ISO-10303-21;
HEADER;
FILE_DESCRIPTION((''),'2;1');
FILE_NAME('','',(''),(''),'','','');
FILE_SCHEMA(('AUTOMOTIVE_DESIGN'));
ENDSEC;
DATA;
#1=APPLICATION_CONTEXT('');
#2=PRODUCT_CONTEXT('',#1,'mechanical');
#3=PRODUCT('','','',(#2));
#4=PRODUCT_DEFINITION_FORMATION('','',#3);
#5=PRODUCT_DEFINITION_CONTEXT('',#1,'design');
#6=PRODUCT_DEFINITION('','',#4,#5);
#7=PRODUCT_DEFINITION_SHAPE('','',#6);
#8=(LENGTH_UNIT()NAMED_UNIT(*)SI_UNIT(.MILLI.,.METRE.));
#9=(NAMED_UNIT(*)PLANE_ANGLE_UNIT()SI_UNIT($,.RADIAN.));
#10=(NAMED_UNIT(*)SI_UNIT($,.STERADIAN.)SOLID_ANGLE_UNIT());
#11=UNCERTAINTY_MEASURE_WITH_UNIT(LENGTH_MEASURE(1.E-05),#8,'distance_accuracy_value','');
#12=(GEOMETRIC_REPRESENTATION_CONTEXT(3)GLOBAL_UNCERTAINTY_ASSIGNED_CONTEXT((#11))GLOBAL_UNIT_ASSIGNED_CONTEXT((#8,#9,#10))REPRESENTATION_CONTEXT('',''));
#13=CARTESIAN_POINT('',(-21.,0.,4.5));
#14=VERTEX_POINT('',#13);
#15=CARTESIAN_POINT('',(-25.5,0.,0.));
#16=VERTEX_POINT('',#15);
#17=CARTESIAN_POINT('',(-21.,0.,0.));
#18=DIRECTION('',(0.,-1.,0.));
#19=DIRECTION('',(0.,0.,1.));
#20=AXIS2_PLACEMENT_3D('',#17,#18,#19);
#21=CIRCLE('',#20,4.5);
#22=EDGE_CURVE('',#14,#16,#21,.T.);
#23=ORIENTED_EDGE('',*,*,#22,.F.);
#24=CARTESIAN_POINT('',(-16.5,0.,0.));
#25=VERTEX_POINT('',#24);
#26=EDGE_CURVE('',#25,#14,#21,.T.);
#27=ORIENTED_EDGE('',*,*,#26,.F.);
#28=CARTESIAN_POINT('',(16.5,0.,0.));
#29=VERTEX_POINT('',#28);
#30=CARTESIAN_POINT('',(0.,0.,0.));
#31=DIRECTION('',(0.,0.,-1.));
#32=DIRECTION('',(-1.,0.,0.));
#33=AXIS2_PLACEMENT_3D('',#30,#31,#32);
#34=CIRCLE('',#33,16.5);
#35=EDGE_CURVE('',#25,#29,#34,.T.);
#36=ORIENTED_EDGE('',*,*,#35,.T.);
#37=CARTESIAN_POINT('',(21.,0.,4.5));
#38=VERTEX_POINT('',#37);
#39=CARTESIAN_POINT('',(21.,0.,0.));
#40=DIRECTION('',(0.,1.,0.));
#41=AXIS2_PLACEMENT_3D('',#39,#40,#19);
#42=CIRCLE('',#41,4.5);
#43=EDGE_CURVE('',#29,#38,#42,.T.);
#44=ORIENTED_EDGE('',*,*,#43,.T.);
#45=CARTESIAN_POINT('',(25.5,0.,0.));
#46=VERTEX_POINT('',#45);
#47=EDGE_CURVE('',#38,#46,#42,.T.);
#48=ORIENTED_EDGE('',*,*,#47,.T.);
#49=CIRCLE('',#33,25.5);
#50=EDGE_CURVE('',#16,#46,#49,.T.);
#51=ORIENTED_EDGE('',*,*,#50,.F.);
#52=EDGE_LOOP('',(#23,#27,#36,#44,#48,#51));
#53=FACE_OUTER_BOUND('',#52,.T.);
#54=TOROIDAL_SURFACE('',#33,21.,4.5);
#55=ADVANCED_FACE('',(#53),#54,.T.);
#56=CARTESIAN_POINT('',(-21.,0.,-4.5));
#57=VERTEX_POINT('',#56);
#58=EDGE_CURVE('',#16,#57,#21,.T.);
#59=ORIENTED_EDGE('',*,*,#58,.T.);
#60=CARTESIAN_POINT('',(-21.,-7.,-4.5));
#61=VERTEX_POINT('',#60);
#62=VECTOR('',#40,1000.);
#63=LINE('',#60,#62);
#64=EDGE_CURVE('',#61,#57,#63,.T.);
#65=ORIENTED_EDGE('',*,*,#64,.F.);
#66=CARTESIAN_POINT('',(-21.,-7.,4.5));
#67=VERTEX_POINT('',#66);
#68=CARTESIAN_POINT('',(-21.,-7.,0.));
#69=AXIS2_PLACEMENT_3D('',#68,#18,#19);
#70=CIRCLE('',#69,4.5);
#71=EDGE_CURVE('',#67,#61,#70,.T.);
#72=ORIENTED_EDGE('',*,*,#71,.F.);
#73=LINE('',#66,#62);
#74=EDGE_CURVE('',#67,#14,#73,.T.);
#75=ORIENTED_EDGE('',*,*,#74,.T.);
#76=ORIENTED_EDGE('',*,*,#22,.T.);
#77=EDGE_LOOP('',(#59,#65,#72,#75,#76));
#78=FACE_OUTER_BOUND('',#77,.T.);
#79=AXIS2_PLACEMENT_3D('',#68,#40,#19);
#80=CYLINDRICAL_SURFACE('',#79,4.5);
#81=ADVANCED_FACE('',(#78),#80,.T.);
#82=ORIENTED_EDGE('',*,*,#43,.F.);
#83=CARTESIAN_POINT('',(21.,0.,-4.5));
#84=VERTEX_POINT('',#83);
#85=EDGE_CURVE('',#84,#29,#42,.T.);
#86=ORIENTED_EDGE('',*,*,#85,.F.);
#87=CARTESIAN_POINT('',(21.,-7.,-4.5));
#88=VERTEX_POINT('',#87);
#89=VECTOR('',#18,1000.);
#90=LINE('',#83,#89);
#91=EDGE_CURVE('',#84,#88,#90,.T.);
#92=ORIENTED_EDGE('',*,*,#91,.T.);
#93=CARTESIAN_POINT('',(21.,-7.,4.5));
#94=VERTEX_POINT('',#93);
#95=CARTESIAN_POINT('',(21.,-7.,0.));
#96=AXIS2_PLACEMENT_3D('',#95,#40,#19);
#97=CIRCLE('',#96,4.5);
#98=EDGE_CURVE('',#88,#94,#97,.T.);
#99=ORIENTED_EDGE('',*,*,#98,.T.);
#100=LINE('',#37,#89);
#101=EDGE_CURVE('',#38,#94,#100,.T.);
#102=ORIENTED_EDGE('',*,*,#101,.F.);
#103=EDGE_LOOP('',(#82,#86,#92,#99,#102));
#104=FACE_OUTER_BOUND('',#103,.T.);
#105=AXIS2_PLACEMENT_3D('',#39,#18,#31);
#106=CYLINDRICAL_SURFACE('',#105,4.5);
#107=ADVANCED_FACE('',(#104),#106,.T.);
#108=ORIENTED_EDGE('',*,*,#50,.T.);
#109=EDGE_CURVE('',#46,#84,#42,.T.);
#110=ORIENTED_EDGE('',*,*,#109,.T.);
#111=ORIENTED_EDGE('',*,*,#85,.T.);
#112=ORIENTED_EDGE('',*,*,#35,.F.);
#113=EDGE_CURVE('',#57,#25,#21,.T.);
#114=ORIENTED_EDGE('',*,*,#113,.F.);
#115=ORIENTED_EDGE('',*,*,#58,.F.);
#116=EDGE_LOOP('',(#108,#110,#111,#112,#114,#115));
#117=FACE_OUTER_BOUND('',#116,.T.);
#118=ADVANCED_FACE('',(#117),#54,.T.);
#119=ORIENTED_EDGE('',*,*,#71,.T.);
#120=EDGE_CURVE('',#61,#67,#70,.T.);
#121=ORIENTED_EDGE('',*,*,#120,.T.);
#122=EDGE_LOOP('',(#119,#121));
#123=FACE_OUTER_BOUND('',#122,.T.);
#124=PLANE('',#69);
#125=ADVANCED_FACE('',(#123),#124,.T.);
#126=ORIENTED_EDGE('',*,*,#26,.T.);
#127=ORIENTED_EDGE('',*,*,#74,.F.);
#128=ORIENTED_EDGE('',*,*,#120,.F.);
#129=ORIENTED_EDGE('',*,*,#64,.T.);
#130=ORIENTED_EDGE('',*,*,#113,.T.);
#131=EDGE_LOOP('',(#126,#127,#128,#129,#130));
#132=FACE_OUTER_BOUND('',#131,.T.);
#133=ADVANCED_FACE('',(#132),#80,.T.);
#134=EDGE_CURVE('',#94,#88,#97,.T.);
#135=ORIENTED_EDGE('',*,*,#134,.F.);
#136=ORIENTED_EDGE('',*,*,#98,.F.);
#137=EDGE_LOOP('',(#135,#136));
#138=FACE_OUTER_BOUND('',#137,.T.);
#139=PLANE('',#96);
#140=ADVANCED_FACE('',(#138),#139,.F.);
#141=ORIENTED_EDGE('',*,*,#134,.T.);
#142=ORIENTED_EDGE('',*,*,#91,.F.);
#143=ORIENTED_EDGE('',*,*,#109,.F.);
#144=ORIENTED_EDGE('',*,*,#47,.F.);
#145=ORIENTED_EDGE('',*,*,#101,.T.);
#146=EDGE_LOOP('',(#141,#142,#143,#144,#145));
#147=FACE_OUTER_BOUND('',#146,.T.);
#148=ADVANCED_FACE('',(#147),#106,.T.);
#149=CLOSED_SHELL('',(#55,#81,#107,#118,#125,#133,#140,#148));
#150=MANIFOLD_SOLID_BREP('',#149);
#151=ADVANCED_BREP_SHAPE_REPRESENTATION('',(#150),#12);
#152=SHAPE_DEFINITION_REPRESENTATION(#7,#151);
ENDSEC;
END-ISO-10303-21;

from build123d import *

# Parameters (mm, degrees)
SKETCH4_R = 4.5


with BuildPart() as part:
    # Sweep1: sweep along a path in Sketch1
    with BuildLine(Plane.XY) as sweep1_path:
        Line((-21, -7), (-21, 0))
        ThreePointArc((-21, 0), (0, 21), (21, 0))
        Line((21, 0), (21, -7))
    # Sketch4 → Sweep1 (sweep)
    with BuildSketch(Plane(origin=(0, -7, 0), x_dir=(1, 0, 0), z_dir=(0, 1, 0))):
        with Locations((21, 0)):
            Circle(SKETCH4_R)
    sweep(path=sweep1_path.line)


solid = part.part
